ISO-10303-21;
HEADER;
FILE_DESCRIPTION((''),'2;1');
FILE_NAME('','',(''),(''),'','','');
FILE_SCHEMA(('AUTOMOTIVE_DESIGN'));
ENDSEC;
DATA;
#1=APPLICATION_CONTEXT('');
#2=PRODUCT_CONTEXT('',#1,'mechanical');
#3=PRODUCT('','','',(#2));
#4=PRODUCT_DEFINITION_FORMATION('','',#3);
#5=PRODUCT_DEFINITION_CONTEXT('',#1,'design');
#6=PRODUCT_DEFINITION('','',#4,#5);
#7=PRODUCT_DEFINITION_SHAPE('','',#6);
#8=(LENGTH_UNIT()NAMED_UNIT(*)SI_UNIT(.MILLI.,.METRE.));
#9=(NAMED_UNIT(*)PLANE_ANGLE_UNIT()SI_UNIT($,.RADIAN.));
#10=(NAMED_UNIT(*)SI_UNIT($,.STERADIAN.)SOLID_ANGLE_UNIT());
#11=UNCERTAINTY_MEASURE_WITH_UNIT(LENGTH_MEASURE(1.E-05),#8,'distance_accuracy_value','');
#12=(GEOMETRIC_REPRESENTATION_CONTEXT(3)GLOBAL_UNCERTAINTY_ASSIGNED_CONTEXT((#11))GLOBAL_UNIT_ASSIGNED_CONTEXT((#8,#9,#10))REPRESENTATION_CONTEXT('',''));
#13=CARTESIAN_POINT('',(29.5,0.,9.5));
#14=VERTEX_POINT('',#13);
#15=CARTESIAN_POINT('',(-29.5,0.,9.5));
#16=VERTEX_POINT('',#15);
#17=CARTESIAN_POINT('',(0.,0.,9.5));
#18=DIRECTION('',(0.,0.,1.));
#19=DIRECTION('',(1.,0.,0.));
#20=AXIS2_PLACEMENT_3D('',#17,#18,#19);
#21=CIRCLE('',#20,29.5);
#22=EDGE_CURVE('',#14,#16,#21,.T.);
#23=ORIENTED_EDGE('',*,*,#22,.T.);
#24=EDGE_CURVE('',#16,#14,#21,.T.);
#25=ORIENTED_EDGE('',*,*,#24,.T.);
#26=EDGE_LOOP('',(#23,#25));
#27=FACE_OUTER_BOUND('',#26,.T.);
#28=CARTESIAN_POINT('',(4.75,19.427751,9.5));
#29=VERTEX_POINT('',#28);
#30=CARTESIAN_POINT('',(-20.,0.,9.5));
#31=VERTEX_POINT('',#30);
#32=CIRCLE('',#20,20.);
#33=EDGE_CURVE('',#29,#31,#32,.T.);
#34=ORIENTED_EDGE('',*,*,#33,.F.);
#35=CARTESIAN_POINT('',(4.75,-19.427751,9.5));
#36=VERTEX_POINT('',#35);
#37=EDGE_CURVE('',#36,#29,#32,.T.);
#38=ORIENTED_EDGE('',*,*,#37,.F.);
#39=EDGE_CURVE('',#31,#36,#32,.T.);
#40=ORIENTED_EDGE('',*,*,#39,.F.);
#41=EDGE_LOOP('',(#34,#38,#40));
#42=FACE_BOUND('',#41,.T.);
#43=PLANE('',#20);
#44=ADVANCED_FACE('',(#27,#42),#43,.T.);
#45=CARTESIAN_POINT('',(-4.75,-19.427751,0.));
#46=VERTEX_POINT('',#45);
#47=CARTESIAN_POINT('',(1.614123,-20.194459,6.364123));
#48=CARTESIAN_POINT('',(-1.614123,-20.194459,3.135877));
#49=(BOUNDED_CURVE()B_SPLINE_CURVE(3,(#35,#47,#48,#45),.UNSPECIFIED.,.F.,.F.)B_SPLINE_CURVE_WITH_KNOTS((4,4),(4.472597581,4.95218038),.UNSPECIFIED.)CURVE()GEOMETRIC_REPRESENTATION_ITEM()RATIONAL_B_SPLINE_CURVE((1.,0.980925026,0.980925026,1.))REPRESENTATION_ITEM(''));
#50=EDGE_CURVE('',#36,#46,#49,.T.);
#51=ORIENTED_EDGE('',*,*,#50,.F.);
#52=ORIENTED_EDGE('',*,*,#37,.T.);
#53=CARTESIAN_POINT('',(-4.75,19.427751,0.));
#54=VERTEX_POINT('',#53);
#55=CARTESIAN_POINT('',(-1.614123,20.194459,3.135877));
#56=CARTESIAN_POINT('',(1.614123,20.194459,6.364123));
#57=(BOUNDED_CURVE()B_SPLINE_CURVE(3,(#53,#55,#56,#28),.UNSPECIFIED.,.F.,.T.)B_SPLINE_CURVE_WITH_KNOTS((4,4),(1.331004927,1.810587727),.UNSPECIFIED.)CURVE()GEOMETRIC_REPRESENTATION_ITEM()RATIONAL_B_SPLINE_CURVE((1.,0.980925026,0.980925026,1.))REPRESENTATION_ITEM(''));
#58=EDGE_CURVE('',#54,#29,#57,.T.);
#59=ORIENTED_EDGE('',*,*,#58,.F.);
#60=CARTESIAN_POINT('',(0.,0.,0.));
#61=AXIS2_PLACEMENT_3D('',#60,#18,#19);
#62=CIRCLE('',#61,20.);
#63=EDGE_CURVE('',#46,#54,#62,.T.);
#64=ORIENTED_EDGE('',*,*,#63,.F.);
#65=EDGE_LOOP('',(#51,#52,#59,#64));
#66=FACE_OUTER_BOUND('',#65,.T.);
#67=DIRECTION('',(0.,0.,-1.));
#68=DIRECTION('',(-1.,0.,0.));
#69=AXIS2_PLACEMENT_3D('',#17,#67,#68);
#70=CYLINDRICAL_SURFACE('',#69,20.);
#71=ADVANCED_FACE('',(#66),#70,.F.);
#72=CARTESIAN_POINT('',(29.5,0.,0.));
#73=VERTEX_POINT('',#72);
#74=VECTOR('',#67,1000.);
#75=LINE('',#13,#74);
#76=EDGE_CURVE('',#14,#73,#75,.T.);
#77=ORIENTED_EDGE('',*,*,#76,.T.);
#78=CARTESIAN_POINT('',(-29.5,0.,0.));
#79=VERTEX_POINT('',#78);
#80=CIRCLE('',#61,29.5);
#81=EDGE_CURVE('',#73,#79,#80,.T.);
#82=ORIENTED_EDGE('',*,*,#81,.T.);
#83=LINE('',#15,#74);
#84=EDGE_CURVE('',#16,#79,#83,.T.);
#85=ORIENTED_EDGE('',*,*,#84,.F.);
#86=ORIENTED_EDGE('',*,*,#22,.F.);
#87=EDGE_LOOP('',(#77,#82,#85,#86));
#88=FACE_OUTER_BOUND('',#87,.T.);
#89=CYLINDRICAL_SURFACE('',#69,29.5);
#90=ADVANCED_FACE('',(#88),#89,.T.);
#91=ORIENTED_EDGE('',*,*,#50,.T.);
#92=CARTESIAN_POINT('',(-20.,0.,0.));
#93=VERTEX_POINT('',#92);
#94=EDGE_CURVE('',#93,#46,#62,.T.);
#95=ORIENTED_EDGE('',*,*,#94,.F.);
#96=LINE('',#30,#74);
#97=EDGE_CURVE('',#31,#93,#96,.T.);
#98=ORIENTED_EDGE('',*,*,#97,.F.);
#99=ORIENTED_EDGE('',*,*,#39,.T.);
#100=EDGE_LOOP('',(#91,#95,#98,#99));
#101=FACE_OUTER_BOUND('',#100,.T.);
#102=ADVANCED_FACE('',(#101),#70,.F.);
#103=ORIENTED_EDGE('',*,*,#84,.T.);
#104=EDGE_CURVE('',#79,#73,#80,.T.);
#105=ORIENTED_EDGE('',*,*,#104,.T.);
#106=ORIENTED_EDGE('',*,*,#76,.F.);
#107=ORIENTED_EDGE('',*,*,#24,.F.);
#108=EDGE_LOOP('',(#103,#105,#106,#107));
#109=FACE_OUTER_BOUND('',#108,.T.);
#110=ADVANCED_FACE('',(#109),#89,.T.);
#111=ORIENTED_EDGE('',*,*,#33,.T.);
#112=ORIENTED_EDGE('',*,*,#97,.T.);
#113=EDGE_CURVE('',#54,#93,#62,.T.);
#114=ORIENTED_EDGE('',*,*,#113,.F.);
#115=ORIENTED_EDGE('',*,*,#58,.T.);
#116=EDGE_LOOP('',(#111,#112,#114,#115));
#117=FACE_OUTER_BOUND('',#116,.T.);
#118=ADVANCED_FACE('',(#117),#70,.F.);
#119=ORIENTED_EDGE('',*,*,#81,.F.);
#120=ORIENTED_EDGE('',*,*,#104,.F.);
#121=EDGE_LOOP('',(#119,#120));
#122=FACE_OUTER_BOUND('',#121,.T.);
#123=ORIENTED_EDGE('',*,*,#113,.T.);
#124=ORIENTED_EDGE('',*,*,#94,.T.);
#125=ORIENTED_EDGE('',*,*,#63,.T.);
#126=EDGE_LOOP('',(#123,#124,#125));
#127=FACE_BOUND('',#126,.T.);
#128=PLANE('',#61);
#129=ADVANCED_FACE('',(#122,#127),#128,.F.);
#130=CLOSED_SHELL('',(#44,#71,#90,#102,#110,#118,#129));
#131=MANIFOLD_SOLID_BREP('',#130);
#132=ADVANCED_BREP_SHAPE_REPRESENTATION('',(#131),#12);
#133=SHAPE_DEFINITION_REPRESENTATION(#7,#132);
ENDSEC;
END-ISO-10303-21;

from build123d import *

# Parameters (mm, degrees)
SKETCH1_R           = 29.5
SKETCH1_R_2         = 20
BOSS_EXTRUDE1_DEPTH = 9.5


with BuildPart() as part:
    # Sketch1 → Boss-Extrude1 (new body)
    with BuildSketch(Plane.XY):
        Circle(SKETCH1_R)
        Circle(SKETCH1_R_2, mode=Mode.SUBTRACT)
    extrude(amount=BOSS_EXTRUDE1_DEPTH)


solid = part.part
